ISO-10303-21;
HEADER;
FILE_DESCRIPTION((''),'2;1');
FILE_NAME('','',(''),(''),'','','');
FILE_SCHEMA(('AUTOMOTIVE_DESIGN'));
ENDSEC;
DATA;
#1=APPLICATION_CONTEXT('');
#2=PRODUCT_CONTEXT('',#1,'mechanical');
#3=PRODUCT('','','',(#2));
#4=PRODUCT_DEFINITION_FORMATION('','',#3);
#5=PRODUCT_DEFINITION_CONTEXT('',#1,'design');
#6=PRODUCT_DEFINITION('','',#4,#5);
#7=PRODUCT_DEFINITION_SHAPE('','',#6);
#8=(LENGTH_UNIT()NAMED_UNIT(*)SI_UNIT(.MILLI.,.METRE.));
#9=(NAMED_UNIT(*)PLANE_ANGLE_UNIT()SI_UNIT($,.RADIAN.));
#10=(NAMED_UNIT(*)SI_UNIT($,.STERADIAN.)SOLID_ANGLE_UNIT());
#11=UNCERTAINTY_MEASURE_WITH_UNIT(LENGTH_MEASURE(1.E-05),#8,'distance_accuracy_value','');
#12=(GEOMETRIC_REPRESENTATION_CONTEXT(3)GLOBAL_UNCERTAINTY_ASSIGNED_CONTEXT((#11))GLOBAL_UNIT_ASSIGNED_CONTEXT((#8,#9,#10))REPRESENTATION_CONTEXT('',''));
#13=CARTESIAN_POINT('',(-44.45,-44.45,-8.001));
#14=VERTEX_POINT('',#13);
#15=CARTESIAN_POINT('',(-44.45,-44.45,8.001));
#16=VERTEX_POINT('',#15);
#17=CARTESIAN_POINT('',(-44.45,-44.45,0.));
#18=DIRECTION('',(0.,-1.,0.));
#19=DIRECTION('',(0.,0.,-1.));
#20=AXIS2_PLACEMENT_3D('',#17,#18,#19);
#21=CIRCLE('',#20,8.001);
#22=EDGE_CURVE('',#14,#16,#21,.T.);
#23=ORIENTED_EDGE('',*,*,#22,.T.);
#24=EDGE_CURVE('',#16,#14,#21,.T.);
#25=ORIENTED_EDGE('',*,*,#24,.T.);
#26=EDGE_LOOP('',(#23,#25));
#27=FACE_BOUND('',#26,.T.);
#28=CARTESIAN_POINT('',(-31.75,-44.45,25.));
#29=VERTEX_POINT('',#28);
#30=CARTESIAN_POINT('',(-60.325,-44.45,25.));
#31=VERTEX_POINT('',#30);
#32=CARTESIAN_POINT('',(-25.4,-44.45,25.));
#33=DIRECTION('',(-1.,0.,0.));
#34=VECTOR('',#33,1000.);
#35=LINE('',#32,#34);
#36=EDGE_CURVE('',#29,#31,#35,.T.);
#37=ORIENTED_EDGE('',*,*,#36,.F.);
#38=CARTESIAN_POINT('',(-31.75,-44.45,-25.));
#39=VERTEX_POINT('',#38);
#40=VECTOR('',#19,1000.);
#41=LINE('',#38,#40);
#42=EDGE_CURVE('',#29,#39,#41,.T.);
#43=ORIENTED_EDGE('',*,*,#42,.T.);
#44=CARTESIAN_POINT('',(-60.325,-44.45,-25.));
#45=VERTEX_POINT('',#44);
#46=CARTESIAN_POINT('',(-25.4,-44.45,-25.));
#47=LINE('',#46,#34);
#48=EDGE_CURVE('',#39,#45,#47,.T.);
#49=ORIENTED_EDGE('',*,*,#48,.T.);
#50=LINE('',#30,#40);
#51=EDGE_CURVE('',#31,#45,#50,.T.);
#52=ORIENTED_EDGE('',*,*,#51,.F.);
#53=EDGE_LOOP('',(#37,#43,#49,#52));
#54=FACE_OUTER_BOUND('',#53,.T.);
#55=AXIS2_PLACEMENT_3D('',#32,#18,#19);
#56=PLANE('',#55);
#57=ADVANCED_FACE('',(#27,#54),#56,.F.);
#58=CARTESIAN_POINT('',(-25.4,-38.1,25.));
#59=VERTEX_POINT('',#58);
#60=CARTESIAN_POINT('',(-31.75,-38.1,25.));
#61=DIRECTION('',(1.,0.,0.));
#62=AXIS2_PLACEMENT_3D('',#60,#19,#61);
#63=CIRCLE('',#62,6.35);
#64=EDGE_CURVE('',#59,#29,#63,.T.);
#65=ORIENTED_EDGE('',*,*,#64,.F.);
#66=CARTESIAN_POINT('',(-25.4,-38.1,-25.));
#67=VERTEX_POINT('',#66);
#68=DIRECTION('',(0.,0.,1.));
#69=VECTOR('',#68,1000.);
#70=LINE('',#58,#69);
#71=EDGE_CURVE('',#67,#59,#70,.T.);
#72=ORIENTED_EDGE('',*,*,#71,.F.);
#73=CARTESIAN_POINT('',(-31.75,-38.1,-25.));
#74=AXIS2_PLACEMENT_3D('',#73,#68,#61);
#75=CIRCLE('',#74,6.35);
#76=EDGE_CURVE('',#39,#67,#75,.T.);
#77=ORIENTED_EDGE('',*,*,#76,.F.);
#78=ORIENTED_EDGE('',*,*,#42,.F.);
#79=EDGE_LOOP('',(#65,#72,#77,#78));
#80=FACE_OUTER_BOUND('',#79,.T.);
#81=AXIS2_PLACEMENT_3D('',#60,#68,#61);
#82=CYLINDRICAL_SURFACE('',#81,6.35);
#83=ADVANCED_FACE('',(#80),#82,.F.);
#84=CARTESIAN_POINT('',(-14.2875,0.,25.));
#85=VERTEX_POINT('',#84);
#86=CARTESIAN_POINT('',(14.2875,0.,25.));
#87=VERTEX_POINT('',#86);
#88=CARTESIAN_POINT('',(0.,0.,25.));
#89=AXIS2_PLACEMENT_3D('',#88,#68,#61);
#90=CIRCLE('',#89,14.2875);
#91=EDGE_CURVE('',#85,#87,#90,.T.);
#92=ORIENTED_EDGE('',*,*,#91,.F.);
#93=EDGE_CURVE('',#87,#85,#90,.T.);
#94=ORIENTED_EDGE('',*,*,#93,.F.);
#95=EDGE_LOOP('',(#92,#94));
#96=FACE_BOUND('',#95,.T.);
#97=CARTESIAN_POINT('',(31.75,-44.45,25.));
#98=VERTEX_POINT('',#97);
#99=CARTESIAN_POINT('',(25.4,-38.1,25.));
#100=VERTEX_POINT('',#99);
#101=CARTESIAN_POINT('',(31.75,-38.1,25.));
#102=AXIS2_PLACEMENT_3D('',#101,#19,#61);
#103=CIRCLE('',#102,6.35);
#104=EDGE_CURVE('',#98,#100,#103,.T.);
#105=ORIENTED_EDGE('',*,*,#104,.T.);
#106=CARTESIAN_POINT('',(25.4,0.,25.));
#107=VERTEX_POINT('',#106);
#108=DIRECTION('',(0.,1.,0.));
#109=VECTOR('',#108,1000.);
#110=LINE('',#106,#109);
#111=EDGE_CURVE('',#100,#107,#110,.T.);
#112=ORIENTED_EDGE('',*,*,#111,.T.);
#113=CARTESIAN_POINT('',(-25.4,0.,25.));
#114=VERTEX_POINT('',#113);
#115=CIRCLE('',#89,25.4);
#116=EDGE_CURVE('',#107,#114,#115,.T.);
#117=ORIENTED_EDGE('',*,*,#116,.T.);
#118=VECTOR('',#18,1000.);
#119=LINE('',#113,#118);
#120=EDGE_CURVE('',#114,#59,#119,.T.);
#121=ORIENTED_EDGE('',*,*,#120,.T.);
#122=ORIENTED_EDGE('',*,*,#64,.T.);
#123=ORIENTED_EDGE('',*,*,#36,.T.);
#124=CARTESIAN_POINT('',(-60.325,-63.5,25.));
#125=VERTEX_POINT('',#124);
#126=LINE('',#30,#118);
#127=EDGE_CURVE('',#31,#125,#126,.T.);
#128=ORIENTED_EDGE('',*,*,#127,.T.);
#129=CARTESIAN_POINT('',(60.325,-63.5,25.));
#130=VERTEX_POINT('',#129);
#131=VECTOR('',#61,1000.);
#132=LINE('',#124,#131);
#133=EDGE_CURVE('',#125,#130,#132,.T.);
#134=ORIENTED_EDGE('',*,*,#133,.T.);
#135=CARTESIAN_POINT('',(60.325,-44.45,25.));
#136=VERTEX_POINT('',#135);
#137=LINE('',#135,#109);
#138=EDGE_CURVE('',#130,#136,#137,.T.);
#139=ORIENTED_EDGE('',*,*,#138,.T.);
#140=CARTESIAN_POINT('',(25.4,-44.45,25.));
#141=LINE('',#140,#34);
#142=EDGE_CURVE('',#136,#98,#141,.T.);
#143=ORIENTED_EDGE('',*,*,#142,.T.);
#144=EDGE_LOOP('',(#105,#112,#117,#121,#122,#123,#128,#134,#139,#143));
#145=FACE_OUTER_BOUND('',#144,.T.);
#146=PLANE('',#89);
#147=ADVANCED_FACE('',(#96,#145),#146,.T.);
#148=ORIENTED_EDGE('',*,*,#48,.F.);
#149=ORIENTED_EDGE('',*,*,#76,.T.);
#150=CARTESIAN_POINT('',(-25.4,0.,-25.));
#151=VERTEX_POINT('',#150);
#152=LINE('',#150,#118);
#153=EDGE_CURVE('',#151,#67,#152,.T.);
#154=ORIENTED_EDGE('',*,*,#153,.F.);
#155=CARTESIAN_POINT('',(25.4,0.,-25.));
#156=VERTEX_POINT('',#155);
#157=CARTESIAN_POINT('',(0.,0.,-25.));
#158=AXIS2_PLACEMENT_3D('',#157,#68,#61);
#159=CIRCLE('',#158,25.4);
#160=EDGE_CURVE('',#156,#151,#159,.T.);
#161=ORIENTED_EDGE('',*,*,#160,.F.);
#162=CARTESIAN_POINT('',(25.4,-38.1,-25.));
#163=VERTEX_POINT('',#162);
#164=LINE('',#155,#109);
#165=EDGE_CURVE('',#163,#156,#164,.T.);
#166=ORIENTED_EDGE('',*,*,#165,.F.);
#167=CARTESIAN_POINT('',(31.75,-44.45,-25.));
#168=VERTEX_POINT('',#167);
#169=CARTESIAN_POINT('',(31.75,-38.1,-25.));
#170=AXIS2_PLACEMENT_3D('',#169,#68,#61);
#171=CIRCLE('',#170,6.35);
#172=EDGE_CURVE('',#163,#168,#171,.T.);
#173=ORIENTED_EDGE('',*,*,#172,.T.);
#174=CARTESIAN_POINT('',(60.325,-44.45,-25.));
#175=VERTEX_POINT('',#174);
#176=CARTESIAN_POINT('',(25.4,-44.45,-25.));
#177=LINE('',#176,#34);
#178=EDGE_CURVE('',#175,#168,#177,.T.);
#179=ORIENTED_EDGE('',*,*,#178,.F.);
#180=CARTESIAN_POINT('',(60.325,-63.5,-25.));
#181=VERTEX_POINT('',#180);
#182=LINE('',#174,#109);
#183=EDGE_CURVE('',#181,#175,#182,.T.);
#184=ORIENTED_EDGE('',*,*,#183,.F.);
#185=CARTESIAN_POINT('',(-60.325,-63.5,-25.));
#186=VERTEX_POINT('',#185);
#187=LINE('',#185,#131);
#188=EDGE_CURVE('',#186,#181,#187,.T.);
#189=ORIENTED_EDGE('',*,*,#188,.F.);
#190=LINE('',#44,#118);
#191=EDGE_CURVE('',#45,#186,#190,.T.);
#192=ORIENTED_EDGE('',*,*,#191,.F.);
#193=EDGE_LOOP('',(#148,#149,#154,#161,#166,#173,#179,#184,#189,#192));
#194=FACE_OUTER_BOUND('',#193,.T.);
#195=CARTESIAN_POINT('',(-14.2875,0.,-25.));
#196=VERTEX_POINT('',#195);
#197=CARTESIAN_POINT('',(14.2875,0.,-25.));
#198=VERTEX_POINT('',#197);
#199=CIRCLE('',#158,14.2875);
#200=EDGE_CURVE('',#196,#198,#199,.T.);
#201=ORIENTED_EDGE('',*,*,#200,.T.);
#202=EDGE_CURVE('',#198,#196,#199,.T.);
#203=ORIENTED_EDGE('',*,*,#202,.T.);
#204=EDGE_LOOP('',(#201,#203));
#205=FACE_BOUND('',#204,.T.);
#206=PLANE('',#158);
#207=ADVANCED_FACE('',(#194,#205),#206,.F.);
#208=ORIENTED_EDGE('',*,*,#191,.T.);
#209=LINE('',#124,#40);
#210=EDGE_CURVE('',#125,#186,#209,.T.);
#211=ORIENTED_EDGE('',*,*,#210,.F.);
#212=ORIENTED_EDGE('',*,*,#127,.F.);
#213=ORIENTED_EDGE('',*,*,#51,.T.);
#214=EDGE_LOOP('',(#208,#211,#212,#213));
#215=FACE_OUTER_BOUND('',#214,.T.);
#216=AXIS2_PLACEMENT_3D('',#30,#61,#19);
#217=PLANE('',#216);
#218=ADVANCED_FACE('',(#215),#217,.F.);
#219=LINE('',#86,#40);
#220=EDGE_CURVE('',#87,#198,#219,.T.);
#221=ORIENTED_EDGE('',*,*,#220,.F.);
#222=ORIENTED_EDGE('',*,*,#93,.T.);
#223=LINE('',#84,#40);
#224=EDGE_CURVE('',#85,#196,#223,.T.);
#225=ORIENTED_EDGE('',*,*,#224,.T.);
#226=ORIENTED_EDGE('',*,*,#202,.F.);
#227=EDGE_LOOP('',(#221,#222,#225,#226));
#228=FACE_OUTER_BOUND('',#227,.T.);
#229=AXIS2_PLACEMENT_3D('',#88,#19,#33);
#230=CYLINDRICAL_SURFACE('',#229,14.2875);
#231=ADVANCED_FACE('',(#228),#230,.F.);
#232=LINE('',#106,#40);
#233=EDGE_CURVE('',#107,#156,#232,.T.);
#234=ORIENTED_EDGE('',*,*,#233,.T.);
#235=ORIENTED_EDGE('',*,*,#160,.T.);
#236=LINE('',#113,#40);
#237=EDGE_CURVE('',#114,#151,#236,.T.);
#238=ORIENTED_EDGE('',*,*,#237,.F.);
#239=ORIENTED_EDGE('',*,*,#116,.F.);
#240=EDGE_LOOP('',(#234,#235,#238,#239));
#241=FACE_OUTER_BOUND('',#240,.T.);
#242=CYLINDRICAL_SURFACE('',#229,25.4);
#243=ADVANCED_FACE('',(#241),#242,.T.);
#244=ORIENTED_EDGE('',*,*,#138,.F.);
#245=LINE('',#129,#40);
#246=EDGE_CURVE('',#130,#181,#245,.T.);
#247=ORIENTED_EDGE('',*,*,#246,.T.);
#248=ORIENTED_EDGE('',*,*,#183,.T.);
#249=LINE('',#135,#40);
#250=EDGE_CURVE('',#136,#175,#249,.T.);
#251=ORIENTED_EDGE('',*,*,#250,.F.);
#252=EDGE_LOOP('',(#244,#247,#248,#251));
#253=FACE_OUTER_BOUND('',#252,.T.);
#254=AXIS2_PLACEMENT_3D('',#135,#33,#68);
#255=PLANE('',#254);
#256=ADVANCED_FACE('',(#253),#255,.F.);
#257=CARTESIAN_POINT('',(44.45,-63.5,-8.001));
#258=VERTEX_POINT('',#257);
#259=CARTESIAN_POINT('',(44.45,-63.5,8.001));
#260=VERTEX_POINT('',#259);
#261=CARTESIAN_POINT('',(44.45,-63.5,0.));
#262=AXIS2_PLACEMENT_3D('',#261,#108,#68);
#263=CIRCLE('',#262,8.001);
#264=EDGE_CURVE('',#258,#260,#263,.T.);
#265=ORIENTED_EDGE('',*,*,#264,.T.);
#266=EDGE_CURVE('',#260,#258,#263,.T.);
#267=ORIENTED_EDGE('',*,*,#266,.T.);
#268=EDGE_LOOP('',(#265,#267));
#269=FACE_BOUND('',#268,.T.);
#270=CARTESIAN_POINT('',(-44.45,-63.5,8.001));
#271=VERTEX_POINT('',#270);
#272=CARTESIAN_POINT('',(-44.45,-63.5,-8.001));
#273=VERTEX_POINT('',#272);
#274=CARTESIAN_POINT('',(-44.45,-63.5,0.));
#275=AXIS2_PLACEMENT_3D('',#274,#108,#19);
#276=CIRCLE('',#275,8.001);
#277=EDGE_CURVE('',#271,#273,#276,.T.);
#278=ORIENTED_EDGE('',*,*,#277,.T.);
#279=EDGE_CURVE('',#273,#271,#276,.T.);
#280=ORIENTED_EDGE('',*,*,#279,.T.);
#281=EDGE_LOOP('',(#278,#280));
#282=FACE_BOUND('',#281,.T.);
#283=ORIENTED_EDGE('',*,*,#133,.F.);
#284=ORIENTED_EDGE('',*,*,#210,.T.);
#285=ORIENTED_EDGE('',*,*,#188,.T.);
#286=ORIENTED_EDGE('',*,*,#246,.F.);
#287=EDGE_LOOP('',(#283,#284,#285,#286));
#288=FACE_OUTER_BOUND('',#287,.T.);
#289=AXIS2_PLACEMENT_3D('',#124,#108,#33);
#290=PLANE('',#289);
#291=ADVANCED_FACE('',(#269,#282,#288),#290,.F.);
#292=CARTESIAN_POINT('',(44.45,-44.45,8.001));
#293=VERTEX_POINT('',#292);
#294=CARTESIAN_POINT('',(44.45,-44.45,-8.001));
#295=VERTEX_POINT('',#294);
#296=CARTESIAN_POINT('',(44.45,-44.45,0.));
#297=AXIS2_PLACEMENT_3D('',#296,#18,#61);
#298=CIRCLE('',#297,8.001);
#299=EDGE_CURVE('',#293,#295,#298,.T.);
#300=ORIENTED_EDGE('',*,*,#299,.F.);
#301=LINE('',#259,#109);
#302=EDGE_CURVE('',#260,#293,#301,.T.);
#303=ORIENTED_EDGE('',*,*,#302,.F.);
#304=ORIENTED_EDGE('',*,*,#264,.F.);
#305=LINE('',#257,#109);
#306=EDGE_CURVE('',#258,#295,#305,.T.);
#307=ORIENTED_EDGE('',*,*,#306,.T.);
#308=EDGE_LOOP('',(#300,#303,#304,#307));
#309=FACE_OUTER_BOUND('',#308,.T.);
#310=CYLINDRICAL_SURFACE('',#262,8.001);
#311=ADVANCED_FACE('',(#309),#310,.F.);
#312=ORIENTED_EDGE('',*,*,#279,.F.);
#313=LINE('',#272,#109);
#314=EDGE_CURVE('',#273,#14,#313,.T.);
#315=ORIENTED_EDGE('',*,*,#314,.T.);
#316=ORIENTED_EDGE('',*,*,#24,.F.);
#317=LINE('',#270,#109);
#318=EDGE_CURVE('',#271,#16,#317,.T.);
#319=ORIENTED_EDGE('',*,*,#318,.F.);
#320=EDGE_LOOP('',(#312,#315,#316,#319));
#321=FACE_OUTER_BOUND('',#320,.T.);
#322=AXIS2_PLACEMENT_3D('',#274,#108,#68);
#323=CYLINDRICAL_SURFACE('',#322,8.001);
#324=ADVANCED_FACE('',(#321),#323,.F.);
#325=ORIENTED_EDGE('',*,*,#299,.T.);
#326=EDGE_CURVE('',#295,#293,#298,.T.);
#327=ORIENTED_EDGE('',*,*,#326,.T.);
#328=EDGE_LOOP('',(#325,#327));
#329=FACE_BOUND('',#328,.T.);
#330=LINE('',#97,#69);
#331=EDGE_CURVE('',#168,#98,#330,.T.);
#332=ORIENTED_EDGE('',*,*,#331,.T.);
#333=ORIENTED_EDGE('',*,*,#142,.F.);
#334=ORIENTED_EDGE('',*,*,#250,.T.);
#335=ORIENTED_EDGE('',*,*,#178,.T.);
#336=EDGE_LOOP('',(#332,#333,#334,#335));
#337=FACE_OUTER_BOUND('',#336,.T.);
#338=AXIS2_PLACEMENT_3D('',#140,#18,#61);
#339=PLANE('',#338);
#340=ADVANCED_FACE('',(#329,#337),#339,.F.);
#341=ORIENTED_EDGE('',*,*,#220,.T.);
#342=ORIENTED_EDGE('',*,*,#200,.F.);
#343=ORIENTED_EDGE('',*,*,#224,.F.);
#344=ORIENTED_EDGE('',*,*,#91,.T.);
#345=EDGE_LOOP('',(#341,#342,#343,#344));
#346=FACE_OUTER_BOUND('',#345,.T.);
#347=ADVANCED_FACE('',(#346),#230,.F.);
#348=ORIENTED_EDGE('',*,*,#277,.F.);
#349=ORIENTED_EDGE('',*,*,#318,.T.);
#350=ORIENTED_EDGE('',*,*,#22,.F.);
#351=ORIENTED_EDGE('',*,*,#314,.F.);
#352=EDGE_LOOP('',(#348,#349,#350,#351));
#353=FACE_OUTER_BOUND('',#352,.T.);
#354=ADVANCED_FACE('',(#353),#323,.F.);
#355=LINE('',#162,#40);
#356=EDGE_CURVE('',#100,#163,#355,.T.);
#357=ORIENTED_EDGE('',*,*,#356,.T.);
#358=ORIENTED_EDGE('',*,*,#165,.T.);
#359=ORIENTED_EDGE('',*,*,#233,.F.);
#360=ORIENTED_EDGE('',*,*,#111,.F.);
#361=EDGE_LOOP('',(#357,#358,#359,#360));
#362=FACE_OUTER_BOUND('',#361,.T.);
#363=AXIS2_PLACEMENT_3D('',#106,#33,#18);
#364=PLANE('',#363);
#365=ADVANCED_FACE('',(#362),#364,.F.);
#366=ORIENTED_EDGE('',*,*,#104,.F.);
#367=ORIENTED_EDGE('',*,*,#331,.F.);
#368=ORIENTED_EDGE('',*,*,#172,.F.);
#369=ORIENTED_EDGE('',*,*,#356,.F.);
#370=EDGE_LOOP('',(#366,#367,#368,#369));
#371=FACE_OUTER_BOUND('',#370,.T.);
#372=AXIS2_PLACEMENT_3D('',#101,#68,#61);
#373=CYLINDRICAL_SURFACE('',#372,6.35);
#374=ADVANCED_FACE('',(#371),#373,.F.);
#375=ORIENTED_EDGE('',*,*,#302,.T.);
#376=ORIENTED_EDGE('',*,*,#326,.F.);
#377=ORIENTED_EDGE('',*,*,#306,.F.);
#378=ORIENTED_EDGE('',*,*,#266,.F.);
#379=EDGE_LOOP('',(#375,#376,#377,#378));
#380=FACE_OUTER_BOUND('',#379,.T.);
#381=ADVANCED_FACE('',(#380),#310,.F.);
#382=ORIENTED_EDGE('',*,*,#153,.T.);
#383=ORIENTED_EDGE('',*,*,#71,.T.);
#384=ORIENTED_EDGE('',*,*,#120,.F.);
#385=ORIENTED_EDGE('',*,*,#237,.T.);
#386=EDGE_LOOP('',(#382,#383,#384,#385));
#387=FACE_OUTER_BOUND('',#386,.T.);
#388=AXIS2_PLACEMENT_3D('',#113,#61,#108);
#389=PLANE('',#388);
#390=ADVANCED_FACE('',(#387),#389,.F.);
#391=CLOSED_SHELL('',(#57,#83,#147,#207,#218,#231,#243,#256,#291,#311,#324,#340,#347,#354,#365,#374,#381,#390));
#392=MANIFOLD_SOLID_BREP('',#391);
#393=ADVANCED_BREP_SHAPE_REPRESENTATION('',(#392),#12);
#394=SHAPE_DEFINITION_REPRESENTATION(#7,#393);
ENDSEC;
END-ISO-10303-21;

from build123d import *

# Parameters (mm, degrees)
SKETCH1_R          = 14.2875
EXTRUDE1_DEPTH     = 25
FILLET1_R          = 6.35
SKETCH2_R          = 8.001
CUT_EXTRUDE1_DEPTH = 92.084332489


with BuildPart() as part:
    # Sketch1 → Extrude1 (new, symmetric)
    with BuildSketch(Plane.XY):
        with BuildLine():
            Line((-25.4, 0), (-25.4, -44.45))
            Line((-25.4, -44.45), (-60.325, -44.45))
            Line((-60.325, -44.45), (-60.325, -63.5))
            Line((-60.325, -63.5), (60.325, -63.5))
            Line((60.325, -63.5), (60.325, -44.45))
            Line((60.325, -44.45), (25.4, -44.45))
            Line((25.4, -44.45), (25.4, 0))
            ThreePointArc((25.4, 0), (0, 25.4), (-25.4, 0))
        make_face()
        Circle(SKETCH1_R, mode=Mode.SUBTRACT)
    extrude(amount=EXTRUDE1_DEPTH, both=True)

    # Fillet1
    fillet1_edges = [part.edges().sort_by_distance(p)[0] for p in [
        (25.4, -44.45, 0),
        (-25.4, -44.45, 0),
    ]]
    fillet(fillet1_edges, radius=FILLET1_R)

    # Sketch2 → Cut-Extrude1 (cut, through all)
    with BuildSketch(Plane(origin=(0, 0, 0), x_dir=(1, 0, 0), z_dir=(0, 1, 0))):
        with Locations(Location((44.45, 0, 0), (0, 0, 270))):
            Circle(SKETCH2_R)
        with Locations(Location((-44.45, 0, 0), (0, 0, 90))):
            Circle(SKETCH2_R)
    extrude(amount=-CUT_EXTRUDE1_DEPTH, mode=Mode.SUBTRACT)


solid = part.part
